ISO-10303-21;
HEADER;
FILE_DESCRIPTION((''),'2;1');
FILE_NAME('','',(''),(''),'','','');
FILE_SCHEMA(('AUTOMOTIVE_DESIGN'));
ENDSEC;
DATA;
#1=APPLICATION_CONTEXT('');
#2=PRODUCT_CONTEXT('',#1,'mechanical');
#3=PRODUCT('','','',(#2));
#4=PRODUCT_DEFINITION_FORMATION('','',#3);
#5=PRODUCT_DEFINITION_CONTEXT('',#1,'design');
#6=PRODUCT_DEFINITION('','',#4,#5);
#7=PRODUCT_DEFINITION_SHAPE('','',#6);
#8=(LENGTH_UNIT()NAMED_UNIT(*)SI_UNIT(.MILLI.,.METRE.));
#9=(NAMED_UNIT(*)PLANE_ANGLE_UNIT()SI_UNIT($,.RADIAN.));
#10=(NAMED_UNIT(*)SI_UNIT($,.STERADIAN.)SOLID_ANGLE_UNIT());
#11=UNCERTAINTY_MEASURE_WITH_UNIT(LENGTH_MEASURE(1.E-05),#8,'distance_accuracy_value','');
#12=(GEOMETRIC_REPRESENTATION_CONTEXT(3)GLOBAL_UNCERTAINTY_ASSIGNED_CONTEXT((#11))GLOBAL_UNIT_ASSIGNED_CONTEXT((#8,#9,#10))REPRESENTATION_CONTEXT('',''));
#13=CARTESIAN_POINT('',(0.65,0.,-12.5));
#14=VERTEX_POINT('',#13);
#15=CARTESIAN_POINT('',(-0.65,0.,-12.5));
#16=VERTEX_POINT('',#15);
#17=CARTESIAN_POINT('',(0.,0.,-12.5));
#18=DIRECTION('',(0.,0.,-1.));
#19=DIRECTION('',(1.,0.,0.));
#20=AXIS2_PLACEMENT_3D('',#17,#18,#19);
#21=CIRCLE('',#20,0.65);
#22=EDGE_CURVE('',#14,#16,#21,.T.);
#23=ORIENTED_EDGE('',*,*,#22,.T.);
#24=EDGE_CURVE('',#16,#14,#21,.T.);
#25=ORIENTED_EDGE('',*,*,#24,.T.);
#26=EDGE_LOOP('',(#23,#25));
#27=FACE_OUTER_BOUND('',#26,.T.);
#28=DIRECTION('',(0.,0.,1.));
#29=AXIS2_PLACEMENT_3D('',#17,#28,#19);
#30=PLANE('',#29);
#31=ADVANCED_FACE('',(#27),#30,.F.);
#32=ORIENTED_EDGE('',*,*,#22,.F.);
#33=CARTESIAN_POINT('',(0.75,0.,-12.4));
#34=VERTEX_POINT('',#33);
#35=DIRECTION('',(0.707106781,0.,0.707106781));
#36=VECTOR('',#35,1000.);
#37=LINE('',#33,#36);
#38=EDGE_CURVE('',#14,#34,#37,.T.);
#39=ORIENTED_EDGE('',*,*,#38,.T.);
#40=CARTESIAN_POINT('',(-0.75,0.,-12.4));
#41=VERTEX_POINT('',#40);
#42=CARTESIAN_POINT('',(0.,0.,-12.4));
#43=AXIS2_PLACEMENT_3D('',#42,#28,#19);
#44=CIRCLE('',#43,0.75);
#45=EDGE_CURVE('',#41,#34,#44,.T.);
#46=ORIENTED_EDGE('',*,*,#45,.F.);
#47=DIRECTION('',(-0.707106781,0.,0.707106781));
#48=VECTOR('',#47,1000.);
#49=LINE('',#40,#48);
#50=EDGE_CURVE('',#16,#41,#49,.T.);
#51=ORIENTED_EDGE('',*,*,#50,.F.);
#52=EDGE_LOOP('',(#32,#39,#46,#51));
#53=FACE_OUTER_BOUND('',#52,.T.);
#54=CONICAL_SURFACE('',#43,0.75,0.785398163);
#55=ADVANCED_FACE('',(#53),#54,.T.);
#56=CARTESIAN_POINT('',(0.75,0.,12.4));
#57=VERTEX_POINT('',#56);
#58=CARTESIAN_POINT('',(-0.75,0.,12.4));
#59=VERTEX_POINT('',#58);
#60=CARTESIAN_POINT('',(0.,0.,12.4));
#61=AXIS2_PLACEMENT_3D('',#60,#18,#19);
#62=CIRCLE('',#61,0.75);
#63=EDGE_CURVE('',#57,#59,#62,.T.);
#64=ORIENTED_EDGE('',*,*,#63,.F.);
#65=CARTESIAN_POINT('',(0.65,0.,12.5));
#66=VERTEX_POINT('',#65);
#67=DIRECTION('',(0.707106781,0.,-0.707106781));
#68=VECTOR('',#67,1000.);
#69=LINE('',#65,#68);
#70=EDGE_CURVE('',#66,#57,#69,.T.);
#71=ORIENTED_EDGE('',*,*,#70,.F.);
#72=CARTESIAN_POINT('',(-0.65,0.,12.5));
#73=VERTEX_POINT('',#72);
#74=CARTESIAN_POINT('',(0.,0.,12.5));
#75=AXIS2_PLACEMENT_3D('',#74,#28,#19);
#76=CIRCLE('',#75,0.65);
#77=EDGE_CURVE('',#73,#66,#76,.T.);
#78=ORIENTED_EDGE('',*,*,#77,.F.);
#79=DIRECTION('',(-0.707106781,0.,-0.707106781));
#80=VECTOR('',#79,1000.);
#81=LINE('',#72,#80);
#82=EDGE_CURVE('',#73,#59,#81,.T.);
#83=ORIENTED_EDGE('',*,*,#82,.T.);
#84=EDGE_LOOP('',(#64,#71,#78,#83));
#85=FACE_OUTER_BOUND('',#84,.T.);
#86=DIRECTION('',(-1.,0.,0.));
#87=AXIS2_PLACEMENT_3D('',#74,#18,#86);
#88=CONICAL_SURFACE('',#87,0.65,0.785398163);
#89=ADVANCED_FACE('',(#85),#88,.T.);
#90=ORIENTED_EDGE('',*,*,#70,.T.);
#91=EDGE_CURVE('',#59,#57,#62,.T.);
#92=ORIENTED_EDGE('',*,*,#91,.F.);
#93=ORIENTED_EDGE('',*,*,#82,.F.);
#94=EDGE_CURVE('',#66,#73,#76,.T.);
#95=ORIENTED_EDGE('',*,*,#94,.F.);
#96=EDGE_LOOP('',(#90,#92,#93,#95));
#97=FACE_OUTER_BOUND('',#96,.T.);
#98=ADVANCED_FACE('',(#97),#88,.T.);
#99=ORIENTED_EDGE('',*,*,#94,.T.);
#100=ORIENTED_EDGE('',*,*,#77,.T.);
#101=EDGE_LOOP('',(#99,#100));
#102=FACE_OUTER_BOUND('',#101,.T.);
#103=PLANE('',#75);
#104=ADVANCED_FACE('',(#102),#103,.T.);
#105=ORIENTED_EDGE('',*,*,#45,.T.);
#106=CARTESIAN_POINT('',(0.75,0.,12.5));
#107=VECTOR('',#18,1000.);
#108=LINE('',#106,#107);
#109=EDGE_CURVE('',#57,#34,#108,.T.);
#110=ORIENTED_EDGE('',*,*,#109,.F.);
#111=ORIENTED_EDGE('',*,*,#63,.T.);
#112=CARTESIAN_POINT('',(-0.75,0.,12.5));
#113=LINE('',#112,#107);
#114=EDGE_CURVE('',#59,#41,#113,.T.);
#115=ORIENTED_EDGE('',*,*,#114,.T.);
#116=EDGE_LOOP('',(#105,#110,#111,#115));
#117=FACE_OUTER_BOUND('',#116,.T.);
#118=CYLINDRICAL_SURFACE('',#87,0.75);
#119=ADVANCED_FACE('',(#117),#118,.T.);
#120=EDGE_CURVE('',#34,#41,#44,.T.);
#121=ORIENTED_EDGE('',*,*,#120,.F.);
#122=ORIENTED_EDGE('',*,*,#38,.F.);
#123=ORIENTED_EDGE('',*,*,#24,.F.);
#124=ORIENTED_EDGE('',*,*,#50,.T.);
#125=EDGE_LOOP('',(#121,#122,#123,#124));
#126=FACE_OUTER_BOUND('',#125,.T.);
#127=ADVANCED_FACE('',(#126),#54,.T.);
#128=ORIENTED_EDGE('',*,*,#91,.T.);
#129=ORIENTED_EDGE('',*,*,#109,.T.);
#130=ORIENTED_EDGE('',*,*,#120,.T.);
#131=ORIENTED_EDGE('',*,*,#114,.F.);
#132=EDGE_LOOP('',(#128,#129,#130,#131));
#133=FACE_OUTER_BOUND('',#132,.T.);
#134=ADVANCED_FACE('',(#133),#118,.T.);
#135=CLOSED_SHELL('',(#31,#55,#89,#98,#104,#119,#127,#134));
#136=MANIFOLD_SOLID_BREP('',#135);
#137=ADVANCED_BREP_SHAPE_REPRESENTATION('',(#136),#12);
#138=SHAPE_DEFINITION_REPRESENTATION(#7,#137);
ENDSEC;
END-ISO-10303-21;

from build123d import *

# Parameters (mm, degrees)
SKETCH1_R           = 0.75
BOSS_EXTRUDE1_DEPTH = 12.5
CHAMFER1_SIZE       = 0.1


with BuildPart() as part:
    # Sketch1 → Boss-Extrude1 (new, symmetric)
    with BuildSketch(Plane.XY):
        Circle(SKETCH1_R)
    extrude(amount=BOSS_EXTRUDE1_DEPTH, both=True)

    # Chamfer1
    chamfer1_edges = [part.edges().sort_by_distance(p)[0] for p in [
        (-0.75, 0, -12.5),
        (-0.75, 0, 12.5),
    ]]
    chamfer(chamfer1_edges, length=CHAMFER1_SIZE)


solid = part.part
